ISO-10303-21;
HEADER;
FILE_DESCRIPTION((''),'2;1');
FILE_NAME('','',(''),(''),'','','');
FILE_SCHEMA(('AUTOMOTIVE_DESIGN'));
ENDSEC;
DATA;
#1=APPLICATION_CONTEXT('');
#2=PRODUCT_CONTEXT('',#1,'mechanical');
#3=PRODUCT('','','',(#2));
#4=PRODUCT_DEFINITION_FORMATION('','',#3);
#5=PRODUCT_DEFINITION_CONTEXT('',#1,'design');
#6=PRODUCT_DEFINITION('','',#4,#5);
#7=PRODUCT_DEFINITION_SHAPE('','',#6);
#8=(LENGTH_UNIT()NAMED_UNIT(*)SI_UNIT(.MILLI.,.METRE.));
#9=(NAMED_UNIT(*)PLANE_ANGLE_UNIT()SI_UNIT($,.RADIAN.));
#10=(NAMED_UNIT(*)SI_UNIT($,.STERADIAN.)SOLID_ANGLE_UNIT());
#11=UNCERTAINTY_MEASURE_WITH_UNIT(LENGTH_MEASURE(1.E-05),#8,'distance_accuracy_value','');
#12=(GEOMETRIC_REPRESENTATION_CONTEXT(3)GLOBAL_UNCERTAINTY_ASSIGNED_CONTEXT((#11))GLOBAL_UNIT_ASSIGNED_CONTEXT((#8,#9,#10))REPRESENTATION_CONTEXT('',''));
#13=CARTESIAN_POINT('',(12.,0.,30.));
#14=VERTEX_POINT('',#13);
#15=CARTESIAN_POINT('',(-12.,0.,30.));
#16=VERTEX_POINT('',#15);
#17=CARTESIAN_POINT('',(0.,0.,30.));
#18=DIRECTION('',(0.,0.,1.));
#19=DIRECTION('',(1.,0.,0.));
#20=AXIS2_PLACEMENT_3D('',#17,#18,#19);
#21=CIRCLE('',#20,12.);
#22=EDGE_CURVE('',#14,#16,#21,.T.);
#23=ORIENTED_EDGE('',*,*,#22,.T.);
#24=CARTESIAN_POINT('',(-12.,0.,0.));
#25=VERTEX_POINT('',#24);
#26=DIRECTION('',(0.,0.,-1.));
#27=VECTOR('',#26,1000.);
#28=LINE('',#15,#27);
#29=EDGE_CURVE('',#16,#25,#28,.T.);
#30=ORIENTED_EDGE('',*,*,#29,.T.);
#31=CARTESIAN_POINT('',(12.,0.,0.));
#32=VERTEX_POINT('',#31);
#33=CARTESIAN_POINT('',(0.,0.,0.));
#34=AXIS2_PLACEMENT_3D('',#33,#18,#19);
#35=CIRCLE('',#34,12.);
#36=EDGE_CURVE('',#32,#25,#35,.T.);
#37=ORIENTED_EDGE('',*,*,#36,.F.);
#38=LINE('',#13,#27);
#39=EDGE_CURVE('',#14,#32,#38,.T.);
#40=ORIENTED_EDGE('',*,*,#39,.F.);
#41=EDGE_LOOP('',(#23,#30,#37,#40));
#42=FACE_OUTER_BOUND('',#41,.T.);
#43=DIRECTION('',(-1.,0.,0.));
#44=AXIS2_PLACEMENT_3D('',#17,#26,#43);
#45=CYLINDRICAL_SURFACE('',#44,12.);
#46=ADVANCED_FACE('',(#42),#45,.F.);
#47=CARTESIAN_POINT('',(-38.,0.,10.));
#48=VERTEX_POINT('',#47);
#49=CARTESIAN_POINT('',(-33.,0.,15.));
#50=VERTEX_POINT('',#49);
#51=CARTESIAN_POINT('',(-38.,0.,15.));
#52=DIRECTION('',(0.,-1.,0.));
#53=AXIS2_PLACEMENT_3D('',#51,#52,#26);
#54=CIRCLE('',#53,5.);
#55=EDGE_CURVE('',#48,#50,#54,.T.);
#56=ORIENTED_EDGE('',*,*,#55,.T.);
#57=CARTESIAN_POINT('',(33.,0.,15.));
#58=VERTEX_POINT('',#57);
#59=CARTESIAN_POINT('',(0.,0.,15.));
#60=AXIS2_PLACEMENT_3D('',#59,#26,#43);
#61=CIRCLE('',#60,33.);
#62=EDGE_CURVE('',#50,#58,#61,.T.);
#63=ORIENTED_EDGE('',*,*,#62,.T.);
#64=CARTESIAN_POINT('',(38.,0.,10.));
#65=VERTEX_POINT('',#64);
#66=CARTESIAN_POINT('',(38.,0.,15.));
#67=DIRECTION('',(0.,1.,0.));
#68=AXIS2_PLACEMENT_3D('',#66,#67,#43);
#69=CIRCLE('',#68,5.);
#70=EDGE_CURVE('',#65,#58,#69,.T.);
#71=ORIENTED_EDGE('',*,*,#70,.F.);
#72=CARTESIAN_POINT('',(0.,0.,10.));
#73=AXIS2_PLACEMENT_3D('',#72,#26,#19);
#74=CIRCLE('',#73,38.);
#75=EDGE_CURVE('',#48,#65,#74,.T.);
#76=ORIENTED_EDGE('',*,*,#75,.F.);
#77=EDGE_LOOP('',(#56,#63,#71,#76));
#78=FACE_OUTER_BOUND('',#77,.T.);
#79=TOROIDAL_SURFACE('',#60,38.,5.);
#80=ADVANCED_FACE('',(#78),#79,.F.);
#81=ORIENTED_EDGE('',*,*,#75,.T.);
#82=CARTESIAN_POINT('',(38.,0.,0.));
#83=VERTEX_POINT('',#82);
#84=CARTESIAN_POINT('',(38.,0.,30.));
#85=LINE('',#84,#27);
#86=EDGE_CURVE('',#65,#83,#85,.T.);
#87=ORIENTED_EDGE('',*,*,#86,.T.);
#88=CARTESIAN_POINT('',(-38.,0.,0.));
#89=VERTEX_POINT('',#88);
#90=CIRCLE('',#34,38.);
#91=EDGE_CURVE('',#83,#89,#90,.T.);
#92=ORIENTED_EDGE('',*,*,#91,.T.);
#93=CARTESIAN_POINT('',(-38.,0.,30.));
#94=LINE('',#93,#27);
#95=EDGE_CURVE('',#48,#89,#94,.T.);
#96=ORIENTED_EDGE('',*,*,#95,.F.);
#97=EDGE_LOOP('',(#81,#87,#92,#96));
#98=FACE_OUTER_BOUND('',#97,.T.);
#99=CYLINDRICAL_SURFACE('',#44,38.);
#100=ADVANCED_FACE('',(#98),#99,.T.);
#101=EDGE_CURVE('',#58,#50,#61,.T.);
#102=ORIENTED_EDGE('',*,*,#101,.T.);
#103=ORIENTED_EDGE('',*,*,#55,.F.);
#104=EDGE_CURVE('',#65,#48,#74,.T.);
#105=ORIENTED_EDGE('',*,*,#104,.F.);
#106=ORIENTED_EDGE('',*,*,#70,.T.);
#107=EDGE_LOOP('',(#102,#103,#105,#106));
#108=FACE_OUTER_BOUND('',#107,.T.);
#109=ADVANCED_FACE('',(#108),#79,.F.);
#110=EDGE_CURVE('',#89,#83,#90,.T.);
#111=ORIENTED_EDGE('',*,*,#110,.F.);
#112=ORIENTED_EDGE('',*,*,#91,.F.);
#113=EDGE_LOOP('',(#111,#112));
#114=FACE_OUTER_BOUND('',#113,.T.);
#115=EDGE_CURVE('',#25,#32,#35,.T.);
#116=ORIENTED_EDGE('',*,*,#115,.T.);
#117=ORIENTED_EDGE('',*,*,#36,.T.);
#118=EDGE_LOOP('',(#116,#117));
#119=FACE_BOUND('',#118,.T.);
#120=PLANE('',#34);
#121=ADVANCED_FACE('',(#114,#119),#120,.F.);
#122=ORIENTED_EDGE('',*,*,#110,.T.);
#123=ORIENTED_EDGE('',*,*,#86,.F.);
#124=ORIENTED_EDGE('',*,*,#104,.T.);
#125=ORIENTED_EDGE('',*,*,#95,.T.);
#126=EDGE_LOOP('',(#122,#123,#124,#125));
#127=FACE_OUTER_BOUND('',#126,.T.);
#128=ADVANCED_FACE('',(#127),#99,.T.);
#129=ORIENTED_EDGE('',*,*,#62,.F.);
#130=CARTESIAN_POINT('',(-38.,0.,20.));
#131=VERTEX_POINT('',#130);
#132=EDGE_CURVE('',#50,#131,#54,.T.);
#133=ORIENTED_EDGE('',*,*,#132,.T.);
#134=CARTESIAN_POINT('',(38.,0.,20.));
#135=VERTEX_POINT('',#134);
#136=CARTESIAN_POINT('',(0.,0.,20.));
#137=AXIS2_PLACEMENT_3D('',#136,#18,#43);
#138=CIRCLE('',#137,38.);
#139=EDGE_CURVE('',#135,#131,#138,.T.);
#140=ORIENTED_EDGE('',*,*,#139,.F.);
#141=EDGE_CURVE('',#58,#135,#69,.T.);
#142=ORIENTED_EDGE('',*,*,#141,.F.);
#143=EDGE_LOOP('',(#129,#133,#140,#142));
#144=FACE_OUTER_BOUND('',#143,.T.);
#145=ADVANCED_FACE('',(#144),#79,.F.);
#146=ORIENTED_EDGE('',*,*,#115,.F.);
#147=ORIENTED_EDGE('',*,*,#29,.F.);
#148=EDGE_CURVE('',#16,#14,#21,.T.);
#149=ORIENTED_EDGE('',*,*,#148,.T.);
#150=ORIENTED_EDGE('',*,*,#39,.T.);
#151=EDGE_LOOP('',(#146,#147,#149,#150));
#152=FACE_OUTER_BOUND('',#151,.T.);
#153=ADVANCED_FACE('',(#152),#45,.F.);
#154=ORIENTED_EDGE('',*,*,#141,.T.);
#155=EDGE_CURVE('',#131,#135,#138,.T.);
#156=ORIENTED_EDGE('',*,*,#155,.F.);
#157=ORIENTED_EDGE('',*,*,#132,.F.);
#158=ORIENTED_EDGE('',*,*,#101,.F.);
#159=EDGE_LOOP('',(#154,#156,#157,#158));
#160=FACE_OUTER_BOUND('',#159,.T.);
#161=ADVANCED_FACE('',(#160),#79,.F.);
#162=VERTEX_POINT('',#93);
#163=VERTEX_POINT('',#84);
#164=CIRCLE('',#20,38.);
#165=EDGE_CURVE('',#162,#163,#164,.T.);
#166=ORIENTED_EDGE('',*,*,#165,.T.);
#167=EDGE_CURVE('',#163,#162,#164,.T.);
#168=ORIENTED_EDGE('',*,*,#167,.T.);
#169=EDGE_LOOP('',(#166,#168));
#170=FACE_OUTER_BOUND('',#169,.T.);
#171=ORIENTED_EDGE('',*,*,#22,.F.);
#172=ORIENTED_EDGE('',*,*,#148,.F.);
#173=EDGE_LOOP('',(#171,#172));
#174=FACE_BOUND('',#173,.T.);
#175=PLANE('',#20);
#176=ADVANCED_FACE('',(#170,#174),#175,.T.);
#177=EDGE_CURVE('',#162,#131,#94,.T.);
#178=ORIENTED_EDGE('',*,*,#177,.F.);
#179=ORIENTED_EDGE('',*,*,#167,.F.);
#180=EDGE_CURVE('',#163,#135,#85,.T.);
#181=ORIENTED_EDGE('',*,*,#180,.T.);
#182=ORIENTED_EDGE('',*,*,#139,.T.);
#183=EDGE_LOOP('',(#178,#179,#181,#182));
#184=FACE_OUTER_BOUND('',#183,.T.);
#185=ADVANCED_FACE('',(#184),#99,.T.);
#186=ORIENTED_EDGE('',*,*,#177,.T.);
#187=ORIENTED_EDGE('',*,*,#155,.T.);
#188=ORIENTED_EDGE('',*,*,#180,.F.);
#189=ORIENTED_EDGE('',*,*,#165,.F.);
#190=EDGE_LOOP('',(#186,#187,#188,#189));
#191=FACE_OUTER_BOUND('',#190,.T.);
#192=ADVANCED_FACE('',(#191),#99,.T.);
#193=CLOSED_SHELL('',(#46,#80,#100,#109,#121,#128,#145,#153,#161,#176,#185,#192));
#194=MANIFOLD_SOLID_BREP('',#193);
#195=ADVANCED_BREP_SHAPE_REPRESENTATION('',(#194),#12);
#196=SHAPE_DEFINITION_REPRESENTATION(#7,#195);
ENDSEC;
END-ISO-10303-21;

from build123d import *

# Parameters (mm, degrees)
SKETCH1_R           = 38
SKETCH1_R_2         = 12
BOSS_EXTRUDE1_DEPTH = 30
SKETCH2_R           = 5


with BuildPart() as part:
    # Sketch1 → Boss-Extrude1 (new body)
    with BuildSketch(Plane.XY):
        Circle(SKETCH1_R)
        Circle(SKETCH1_R_2, mode=Mode.SUBTRACT)
    extrude(amount=BOSS_EXTRUDE1_DEPTH)

    # Sketch2 → Cut-Revolve1 (revolve, cut)
    with BuildSketch(Plane(origin=(0, 0, 0), x_dir=(1, 0, 0), z_dir=(0, 1, 0))):
        with Locations((-38, -15)):
            Circle(SKETCH2_R)
    revolve(axis=Axis((0, 0, 0), (0, 0, 1)), mode=Mode.SUBTRACT)


solid = part.part
